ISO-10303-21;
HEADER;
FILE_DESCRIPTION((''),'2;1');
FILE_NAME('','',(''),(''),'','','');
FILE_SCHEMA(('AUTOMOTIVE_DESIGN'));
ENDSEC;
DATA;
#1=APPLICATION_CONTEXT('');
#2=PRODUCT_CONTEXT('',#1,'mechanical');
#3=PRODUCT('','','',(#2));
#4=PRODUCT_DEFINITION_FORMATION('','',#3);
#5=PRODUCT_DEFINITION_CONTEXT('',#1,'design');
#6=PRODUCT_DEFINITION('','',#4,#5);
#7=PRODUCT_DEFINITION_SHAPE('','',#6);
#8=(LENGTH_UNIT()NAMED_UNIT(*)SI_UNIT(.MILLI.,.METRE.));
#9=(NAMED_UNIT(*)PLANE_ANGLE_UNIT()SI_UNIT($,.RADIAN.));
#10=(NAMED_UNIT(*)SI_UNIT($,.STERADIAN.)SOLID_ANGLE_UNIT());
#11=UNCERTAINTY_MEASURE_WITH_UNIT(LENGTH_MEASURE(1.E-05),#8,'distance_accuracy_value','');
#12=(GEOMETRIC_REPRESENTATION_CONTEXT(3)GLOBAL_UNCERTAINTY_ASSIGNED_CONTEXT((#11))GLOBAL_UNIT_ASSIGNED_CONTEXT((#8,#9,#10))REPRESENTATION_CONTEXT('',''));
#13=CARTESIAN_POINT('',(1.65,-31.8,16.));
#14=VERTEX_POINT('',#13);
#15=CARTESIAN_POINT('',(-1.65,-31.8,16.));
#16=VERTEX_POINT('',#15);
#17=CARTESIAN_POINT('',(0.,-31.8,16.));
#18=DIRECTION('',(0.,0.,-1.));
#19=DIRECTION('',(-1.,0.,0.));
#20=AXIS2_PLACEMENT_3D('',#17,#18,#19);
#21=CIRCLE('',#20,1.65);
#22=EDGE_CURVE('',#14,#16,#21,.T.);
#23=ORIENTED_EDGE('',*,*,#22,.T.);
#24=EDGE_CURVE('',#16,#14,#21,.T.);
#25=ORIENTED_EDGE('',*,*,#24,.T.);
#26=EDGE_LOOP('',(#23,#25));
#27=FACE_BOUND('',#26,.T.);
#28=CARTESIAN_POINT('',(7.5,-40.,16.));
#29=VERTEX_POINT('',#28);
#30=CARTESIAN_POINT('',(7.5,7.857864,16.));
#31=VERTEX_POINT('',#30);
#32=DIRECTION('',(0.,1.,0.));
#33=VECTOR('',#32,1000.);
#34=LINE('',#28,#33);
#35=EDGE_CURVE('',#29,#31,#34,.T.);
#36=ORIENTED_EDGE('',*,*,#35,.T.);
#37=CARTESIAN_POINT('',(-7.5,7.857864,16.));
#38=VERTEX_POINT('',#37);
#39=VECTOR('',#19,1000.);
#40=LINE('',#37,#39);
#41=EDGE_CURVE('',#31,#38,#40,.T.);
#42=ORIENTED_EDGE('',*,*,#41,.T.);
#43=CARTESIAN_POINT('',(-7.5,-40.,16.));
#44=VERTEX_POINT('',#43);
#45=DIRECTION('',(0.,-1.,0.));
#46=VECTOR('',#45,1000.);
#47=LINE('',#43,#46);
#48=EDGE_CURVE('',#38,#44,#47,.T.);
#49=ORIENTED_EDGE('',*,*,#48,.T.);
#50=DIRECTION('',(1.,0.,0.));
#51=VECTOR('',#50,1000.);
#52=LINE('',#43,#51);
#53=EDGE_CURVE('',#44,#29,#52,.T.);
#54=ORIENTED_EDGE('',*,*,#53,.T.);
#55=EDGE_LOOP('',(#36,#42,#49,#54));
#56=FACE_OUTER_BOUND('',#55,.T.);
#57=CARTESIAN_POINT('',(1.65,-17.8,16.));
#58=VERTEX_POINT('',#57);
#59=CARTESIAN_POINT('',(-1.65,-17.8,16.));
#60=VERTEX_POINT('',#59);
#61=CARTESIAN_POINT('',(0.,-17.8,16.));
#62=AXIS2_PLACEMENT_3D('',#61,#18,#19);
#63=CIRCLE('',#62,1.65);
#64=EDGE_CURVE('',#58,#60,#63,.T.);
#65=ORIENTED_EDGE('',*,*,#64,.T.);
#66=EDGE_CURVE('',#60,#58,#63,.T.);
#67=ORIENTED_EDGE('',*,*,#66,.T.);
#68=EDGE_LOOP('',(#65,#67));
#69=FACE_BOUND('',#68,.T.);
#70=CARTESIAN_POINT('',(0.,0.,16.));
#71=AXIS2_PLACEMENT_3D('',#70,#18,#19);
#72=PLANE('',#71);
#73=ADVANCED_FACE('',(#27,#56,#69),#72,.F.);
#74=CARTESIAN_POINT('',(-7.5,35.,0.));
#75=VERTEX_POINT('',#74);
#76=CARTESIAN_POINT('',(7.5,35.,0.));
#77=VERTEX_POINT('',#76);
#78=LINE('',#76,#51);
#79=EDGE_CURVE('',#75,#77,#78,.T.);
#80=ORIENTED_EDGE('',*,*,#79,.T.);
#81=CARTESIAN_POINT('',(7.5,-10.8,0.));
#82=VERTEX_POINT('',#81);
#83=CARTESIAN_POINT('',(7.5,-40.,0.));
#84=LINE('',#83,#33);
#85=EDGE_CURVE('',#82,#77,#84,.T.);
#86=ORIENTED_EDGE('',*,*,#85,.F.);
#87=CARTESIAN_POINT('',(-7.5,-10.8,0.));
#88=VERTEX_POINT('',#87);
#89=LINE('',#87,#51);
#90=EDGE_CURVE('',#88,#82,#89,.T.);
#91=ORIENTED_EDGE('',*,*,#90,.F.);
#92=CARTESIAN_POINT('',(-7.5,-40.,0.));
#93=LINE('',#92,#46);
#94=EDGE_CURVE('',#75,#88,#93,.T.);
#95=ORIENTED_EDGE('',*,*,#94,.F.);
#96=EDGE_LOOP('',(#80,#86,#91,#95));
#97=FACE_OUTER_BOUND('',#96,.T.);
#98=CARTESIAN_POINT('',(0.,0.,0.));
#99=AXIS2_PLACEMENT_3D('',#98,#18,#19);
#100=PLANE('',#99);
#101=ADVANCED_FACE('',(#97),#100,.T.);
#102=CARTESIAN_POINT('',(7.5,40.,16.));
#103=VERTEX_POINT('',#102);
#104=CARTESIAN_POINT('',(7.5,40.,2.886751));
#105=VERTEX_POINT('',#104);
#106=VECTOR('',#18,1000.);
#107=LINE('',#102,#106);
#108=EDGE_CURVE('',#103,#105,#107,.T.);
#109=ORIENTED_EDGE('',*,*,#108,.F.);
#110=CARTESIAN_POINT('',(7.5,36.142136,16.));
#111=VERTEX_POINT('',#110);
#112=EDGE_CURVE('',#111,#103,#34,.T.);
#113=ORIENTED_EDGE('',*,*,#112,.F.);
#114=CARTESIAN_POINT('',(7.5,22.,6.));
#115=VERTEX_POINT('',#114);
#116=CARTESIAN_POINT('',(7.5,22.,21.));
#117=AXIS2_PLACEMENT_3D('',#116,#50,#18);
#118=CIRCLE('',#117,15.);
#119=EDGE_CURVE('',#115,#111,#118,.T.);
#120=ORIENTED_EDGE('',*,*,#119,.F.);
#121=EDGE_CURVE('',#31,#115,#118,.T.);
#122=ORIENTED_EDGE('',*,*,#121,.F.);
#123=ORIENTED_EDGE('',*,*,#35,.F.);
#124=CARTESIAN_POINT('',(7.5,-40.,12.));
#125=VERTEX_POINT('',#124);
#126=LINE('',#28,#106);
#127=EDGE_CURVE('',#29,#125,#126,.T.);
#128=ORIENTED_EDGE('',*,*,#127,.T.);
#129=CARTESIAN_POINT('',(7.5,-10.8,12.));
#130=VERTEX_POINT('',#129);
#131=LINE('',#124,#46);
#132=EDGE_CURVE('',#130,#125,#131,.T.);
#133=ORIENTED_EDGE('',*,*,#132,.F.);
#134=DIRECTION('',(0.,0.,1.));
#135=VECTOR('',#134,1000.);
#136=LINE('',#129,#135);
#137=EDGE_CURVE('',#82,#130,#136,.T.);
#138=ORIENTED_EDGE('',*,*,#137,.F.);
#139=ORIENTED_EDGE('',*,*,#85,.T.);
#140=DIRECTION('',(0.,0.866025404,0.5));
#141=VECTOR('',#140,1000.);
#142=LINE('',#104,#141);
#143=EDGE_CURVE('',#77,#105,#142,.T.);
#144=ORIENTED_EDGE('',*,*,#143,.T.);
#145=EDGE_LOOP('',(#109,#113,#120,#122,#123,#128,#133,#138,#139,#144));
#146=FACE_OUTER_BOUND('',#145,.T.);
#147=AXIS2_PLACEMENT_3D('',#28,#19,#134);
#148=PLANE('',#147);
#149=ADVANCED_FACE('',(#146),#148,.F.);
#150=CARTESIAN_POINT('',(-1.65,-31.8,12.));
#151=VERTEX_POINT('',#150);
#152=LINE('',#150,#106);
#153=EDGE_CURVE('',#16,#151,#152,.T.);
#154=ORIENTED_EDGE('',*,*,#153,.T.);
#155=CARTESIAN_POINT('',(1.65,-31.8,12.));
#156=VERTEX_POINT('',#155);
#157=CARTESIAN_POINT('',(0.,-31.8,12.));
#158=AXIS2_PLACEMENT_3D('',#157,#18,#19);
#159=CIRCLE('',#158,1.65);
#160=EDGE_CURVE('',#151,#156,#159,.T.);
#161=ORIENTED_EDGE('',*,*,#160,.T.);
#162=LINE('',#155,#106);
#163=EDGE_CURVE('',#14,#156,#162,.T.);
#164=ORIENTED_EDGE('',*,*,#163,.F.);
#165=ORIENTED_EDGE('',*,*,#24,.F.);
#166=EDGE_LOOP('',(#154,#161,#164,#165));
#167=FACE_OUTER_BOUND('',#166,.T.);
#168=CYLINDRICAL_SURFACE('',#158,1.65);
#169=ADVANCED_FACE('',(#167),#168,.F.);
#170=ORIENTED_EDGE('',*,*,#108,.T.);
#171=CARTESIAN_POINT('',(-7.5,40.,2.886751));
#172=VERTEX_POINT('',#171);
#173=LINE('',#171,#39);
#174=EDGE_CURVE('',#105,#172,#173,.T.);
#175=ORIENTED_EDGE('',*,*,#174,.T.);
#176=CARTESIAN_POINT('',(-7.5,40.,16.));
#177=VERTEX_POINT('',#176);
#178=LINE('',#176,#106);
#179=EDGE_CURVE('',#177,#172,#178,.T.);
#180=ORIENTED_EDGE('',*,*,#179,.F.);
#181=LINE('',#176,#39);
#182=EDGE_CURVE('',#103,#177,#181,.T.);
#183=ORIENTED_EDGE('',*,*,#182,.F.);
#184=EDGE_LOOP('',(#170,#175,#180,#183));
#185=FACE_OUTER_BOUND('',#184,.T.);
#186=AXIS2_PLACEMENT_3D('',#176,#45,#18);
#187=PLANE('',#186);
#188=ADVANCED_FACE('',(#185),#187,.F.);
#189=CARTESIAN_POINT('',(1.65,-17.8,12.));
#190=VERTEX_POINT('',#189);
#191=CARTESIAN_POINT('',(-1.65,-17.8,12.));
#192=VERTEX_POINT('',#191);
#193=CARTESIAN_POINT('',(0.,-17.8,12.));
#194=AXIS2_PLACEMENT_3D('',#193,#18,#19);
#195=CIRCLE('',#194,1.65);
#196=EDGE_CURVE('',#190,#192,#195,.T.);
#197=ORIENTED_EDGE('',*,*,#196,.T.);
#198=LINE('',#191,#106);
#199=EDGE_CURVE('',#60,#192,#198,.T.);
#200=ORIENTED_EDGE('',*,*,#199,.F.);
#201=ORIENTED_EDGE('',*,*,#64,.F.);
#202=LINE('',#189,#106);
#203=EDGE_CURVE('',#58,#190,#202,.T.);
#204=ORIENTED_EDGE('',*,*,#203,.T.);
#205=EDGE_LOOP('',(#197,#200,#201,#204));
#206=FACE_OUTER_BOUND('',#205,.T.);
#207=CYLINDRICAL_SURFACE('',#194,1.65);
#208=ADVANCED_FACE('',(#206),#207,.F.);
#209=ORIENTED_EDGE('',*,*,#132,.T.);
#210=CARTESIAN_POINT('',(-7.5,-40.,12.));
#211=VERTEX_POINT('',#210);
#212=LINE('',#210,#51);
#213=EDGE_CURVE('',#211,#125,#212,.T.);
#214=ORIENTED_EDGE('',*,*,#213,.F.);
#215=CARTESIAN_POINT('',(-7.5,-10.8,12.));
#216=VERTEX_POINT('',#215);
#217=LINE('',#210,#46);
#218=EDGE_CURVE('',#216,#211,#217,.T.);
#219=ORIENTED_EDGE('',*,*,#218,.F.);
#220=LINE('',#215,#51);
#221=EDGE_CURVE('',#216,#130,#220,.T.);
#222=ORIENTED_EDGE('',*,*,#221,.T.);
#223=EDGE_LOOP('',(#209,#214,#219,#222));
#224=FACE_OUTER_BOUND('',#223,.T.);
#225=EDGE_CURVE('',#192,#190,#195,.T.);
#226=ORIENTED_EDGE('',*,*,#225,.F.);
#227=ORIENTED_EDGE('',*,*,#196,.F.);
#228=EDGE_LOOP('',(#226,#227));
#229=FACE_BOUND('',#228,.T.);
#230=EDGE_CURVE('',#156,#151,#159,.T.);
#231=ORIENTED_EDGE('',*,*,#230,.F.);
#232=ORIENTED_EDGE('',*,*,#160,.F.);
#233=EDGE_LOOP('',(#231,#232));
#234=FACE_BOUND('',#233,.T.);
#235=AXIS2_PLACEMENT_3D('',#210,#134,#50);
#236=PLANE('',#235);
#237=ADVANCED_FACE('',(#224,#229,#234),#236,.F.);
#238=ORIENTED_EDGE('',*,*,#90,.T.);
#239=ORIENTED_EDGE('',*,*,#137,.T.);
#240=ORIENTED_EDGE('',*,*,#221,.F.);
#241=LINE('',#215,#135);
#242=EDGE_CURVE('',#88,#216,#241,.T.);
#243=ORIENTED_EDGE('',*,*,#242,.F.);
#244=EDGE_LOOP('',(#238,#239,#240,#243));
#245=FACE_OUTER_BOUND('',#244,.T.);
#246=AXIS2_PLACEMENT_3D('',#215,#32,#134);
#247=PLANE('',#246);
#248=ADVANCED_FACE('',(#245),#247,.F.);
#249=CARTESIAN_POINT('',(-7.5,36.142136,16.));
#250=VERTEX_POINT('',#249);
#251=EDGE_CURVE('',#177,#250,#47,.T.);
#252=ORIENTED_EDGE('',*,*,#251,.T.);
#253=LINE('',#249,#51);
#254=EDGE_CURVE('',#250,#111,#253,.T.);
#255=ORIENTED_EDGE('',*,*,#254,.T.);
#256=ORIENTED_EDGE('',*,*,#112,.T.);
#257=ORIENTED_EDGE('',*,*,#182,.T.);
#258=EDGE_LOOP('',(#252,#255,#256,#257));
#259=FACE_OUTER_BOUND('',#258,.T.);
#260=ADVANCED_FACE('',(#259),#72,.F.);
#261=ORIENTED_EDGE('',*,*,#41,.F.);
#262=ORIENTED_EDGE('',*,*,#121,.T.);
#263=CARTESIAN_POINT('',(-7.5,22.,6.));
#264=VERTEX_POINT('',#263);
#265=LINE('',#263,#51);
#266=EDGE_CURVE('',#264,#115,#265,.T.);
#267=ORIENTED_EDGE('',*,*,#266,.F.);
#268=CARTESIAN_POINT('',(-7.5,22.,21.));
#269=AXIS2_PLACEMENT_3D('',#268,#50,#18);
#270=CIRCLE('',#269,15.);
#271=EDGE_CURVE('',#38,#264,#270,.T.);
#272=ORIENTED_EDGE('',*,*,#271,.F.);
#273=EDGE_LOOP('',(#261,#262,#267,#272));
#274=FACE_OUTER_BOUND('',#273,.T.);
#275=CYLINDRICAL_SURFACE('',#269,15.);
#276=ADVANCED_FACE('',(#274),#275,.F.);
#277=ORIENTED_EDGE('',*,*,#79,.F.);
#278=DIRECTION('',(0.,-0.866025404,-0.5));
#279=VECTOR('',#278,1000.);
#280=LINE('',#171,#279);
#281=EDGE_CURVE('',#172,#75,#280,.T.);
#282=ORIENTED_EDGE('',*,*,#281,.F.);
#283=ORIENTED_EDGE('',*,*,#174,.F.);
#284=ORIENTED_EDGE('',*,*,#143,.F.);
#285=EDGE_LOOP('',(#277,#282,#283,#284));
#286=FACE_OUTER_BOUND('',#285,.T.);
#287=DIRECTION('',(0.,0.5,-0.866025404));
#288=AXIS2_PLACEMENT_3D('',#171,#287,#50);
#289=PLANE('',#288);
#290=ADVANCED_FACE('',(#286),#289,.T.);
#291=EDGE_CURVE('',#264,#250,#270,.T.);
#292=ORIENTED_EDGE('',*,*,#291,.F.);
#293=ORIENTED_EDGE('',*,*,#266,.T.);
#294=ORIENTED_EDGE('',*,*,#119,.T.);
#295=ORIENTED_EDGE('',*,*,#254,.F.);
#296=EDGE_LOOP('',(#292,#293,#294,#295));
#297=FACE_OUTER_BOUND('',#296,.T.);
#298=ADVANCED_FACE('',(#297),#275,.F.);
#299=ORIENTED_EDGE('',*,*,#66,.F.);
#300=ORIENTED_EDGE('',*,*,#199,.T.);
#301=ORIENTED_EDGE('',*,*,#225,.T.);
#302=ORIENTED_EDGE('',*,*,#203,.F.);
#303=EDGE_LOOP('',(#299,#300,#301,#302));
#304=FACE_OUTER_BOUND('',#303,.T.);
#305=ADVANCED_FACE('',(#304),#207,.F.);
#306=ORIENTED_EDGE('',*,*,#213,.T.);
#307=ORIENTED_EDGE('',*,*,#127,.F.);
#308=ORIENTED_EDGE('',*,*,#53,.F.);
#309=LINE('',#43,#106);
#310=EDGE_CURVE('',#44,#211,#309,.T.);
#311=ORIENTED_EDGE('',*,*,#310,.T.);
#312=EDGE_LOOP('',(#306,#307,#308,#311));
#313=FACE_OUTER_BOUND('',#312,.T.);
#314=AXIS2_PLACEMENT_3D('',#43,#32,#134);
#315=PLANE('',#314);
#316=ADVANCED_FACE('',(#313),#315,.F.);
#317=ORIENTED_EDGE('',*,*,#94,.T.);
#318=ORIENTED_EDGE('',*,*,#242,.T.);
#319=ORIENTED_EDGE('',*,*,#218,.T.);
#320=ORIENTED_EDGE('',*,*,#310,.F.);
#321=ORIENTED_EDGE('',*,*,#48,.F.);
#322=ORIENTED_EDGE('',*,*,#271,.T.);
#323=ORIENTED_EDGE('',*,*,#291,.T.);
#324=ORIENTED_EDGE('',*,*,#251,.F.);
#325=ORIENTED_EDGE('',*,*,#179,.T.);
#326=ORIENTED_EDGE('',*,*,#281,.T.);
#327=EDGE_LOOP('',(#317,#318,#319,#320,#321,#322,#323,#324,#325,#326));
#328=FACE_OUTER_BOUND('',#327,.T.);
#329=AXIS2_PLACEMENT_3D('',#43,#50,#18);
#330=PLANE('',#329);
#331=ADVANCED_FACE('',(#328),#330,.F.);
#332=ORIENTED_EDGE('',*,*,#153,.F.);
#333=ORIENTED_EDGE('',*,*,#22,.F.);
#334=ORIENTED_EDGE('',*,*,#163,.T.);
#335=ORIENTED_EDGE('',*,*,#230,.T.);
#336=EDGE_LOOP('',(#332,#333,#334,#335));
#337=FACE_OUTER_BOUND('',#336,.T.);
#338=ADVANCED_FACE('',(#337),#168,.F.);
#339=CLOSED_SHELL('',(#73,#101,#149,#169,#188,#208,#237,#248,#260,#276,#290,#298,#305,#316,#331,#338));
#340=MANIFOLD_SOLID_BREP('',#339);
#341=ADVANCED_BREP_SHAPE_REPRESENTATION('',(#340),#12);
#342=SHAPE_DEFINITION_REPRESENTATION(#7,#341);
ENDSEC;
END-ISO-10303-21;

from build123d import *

# Parameters (mm, degrees)
SKETCH1_W             = 15
SKETCH1_H             = 80
BOSS_EXTRUDE1_DEPTH   = 16
SKETCH2_W             = 12
SKETCH2_H             = 29.2
CUT_EXTRUDE1_DEPTH    = 46.617978912
M4_TAPPED_HOLE1_D     = 3.3
M4_TAPPED_HOLE1_DEPTH = 22.25
M4_TAPPED_HOLE1_TIP   = 0.991420021
CHAMFER1_SIZE         = 5
CHAMFER1_SIZE2        = 2.886751346
SKETCH6_R             = 15
CUT_EXTRUDE2_DEPTH    = 46.617978912


with BuildPart() as part:
    # Sketch1 → Boss-Extrude1 (new body)
    with BuildSketch(Plane.XY):
        Rectangle(SKETCH1_W, SKETCH1_H)
    extrude(amount=BOSS_EXTRUDE1_DEPTH)

    # Sketch2 → Cut-Extrude1 (cut, through all)
    with BuildSketch(Plane(origin=(7.5, 0, 0), x_dir=(0, 0, -1), z_dir=(1, 0, 0))):
        with Locations((-6, -25.4)):
            Rectangle(SKETCH2_W, SKETCH2_H)
    extrude(amount=-CUT_EXTRUDE1_DEPTH, mode=Mode.SUBTRACT)

    # M4 Tapped Hole1
    with Locations(Plane(origin=(0, 0, 12), x_dir=(-1, 0, 0), z_dir=(0, 0, -1))):
        with Locations((0, -17.8), (0, -31.8)):
            Hole(M4_TAPPED_HOLE1_D / 2, depth=M4_TAPPED_HOLE1_DEPTH)
            with Locations((0, 0, -(M4_TAPPED_HOLE1_DEPTH + M4_TAPPED_HOLE1_TIP / 2))):  # 118° drill point
                Cone(0, M4_TAPPED_HOLE1_D / 2, M4_TAPPED_HOLE1_TIP, mode=Mode.SUBTRACT)

    # Chamfer1
    chamfer1_edges = [part.edges().sort_by_distance(p)[0] for p in [
        (0, 40, 0),
    ]]
    chamfer1_side = [part.faces().sort_by_distance(p)[0] for p in [
        (0, 14.6, 0),
    ]]
    chamfer(chamfer1_edges, length=CHAMFER1_SIZE, length2=CHAMFER1_SIZE2, reference=chamfer1_side[0])

    # Sketch6 → Cut-Extrude2 (cut, through all)
    with BuildSketch(Plane(origin=(7.5, 0, 0), x_dir=(0, 0, -1), z_dir=(1, 0, 0))):
        with Locations((-21, 22)):
            Circle(SKETCH6_R)
    extrude(amount=-CUT_EXTRUDE2_DEPTH, mode=Mode.SUBTRACT)


solid = part.part
